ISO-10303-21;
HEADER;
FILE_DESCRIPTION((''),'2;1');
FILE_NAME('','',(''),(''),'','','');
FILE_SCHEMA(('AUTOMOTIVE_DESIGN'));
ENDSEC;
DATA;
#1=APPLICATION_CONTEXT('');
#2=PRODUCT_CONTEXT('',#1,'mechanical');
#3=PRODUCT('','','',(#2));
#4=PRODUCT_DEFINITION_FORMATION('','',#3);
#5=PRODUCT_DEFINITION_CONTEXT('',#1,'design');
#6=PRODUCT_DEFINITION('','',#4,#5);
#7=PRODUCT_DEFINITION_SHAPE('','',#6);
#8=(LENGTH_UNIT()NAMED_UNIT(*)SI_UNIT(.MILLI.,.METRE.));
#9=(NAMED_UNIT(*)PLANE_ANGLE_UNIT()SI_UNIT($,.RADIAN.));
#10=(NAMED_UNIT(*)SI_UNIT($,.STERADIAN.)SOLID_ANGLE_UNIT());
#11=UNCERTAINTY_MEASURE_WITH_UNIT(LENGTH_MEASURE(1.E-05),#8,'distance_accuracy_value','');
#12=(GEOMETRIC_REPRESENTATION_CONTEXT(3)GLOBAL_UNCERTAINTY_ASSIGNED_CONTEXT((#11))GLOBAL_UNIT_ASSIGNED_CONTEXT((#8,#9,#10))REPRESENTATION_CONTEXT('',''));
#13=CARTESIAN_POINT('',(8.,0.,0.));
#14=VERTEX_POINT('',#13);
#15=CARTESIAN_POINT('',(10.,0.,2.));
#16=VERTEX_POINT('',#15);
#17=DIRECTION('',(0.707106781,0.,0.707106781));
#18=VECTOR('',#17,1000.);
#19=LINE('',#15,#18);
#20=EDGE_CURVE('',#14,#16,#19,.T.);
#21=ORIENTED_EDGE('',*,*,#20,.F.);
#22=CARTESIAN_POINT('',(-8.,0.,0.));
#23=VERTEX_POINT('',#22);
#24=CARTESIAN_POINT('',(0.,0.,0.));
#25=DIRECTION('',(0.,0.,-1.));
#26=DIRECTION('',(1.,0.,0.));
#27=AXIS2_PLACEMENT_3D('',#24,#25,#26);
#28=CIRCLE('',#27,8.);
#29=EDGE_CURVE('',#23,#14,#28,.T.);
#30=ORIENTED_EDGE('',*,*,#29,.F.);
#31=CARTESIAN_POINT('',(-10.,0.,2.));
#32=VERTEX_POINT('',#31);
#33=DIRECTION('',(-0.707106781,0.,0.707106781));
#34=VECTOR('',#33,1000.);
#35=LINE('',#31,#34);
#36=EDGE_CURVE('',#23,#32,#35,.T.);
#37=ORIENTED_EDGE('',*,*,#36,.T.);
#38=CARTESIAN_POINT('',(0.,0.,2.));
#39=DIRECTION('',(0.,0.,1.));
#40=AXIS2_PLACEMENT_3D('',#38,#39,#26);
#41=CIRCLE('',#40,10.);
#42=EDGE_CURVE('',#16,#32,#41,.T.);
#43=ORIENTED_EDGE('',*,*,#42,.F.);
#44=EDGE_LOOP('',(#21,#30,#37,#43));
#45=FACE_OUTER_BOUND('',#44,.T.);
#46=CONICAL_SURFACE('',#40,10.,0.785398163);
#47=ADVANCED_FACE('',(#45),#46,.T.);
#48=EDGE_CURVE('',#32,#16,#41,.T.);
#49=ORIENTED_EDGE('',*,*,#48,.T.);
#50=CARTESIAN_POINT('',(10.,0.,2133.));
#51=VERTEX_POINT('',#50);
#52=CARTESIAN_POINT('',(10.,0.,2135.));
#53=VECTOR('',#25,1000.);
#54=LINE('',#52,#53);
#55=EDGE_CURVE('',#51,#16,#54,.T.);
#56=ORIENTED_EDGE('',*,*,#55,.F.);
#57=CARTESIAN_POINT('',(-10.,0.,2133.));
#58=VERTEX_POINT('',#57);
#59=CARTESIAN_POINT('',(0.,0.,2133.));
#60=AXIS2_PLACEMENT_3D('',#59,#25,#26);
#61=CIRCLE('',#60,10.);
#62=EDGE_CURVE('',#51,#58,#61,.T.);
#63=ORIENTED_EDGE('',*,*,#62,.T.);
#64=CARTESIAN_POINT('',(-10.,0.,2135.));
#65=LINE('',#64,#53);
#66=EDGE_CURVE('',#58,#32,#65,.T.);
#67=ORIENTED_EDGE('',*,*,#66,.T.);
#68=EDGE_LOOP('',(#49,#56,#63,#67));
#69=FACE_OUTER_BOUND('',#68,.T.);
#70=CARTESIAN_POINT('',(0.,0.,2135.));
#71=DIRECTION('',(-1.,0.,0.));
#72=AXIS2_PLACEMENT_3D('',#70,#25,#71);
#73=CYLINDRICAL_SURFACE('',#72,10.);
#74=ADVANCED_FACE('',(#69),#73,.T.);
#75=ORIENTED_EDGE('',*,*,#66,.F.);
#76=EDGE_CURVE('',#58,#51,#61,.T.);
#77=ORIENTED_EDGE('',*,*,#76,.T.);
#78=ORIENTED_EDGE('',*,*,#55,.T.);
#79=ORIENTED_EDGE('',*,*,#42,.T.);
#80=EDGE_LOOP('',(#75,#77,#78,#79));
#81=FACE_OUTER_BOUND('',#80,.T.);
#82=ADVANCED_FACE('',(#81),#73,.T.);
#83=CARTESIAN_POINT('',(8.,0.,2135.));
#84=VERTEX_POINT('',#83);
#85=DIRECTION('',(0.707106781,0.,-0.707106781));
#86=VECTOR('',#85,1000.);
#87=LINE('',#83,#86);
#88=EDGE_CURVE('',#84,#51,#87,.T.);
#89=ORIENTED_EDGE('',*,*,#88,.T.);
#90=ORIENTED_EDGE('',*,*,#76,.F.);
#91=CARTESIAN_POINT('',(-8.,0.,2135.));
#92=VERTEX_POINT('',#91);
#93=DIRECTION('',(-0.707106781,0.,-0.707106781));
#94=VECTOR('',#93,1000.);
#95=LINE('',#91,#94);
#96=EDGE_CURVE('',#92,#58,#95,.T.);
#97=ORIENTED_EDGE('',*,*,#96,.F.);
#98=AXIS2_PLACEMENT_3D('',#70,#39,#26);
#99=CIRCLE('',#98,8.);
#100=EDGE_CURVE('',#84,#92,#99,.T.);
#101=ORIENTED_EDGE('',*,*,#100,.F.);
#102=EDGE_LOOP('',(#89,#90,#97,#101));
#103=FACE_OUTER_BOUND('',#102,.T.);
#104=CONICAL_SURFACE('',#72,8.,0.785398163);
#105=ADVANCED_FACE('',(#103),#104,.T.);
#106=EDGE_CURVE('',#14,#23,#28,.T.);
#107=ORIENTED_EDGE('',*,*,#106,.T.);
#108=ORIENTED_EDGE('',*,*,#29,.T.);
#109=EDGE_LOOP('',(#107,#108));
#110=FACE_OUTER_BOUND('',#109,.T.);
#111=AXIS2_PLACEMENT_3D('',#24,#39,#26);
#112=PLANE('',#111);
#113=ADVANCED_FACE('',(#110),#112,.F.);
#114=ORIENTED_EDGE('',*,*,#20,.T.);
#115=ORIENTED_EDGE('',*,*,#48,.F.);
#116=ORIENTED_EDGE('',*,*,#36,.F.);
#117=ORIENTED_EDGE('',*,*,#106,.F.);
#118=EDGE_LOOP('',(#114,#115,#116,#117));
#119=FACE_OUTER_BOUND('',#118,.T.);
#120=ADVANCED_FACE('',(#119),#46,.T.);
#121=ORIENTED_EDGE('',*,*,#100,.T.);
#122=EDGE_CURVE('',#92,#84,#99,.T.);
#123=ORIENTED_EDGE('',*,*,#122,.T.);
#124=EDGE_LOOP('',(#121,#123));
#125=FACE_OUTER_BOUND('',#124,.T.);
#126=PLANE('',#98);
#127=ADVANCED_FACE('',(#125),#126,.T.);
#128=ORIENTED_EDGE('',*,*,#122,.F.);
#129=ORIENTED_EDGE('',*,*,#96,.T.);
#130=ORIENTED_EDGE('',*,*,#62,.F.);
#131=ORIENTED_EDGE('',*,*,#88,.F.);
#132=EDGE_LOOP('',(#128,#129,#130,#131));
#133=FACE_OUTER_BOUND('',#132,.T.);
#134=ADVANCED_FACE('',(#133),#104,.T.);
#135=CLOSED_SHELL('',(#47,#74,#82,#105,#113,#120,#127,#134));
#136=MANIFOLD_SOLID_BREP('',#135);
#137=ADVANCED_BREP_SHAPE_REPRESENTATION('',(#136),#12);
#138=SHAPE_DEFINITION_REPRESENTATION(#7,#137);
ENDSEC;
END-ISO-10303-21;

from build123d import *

# Parameters (mm, degrees)
SKETCH_1_R      = 10
EXTRUDE_1_DEPTH = 2135
CHAMFER_1_SIZE  = 2


with BuildPart() as part:
    # 草图1 → 凸台-拉伸1 (new body)
    with BuildSketch(Plane.XY):
        Circle(SKETCH_1_R)
    extrude(amount=EXTRUDE_1_DEPTH)

    # 倒角1
    chamfer_1_edges = [part.edges().sort_by_distance(p)[0] for p in [
        (-10, 0, 0),
        (-10, 0, 2135),
    ]]
    chamfer(chamfer_1_edges, length=CHAMFER_1_SIZE)


solid = part.part
